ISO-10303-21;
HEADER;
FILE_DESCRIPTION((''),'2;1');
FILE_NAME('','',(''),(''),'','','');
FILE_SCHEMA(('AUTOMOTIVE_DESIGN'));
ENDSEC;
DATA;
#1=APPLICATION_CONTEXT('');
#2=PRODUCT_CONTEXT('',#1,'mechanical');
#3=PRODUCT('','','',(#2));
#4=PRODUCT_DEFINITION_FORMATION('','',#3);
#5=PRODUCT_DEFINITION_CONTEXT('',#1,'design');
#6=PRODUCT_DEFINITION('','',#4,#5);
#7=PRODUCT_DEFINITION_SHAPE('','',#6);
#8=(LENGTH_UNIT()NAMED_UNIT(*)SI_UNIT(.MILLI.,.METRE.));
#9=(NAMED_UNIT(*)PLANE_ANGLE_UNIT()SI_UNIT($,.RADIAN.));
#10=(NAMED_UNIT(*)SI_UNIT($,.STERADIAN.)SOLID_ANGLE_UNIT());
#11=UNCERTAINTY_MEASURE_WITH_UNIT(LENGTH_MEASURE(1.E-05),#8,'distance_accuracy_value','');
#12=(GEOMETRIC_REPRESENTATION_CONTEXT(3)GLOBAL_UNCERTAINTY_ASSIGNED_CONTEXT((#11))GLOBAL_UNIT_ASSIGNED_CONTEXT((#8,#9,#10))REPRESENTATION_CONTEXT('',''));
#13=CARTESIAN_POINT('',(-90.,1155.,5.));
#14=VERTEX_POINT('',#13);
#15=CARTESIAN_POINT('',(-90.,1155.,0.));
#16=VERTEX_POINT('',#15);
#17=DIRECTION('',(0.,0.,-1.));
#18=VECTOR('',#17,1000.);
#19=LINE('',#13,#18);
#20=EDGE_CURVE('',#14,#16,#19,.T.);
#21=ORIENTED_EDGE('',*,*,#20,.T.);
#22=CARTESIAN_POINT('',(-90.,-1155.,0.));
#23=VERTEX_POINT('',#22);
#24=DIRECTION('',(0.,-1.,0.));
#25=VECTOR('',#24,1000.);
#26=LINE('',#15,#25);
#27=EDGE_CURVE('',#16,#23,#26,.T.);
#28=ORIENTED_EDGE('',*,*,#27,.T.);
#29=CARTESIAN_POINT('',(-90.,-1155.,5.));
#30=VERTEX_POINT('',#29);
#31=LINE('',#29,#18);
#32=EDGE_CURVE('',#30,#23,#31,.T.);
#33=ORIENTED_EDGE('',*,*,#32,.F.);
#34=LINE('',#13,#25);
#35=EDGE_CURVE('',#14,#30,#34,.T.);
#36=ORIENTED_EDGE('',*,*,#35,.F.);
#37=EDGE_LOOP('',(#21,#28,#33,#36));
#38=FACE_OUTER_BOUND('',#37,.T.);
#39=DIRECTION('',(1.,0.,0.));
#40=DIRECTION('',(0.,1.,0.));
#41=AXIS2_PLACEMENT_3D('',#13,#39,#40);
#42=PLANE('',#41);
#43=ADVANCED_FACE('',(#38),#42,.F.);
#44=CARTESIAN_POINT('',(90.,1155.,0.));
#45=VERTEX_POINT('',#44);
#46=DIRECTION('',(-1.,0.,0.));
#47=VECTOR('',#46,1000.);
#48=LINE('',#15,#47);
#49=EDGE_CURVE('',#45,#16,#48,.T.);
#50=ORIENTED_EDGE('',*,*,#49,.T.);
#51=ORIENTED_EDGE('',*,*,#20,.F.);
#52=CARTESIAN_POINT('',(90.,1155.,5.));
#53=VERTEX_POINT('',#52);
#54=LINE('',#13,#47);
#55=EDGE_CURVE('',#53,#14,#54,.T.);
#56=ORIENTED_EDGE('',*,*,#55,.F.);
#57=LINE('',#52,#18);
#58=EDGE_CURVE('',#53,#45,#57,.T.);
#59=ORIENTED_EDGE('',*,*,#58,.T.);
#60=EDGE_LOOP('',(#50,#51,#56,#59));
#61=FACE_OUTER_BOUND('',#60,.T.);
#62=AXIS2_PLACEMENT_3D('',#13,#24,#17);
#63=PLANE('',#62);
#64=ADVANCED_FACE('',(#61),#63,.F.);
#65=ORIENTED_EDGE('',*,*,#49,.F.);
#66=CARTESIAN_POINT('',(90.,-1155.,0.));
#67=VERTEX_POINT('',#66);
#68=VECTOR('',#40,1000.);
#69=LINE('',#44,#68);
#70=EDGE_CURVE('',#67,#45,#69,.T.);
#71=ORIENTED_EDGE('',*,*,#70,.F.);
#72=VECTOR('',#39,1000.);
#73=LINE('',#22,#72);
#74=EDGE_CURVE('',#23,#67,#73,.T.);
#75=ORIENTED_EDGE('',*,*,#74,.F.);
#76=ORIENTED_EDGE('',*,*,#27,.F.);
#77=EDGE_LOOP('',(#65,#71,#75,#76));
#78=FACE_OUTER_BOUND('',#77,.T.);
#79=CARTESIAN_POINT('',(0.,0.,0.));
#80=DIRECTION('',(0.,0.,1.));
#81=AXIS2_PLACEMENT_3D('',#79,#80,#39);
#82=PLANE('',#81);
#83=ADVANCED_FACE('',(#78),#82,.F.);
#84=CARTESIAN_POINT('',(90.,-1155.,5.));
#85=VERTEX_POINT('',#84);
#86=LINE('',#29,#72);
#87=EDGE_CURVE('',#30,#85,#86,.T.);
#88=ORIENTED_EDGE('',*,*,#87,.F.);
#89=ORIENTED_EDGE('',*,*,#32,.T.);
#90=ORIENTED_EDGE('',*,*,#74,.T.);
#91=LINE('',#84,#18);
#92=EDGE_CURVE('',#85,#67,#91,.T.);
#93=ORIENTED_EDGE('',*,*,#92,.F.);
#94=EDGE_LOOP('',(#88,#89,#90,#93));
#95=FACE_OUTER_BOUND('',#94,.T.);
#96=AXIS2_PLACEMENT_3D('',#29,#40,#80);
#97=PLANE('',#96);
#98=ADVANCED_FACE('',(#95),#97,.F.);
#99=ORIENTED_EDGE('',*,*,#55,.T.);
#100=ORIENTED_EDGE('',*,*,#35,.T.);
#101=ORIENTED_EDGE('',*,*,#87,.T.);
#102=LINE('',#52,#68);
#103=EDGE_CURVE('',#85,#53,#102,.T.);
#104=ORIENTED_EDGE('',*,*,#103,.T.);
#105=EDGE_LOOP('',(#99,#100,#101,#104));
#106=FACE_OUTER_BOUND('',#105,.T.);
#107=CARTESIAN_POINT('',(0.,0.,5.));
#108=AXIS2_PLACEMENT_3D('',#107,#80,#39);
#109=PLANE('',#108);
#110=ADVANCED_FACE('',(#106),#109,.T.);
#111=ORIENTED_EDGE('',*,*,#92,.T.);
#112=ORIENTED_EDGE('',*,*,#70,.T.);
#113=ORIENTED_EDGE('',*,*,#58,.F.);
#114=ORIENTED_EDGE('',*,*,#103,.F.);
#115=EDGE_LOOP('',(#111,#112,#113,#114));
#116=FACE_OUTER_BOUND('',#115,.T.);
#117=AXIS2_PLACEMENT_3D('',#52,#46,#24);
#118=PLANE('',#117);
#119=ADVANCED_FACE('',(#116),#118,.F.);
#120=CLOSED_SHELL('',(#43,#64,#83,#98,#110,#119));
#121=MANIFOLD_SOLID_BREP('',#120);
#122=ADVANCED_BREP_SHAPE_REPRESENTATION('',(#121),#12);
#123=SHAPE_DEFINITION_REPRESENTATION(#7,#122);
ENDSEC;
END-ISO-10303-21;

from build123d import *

# Parameters (mm, degrees)
SKETCH_1_W      = 180
SKETCH_1_H      = 2310
EXTRUDE_1_DEPTH = 5


with BuildPart() as part:
    # 草图1 → 凸台-拉伸1 (new body)
    with BuildSketch(Plane.XY):
        Rectangle(SKETCH_1_W, SKETCH_1_H)
    extrude(amount=EXTRUDE_1_DEPTH)


solid = part.part
